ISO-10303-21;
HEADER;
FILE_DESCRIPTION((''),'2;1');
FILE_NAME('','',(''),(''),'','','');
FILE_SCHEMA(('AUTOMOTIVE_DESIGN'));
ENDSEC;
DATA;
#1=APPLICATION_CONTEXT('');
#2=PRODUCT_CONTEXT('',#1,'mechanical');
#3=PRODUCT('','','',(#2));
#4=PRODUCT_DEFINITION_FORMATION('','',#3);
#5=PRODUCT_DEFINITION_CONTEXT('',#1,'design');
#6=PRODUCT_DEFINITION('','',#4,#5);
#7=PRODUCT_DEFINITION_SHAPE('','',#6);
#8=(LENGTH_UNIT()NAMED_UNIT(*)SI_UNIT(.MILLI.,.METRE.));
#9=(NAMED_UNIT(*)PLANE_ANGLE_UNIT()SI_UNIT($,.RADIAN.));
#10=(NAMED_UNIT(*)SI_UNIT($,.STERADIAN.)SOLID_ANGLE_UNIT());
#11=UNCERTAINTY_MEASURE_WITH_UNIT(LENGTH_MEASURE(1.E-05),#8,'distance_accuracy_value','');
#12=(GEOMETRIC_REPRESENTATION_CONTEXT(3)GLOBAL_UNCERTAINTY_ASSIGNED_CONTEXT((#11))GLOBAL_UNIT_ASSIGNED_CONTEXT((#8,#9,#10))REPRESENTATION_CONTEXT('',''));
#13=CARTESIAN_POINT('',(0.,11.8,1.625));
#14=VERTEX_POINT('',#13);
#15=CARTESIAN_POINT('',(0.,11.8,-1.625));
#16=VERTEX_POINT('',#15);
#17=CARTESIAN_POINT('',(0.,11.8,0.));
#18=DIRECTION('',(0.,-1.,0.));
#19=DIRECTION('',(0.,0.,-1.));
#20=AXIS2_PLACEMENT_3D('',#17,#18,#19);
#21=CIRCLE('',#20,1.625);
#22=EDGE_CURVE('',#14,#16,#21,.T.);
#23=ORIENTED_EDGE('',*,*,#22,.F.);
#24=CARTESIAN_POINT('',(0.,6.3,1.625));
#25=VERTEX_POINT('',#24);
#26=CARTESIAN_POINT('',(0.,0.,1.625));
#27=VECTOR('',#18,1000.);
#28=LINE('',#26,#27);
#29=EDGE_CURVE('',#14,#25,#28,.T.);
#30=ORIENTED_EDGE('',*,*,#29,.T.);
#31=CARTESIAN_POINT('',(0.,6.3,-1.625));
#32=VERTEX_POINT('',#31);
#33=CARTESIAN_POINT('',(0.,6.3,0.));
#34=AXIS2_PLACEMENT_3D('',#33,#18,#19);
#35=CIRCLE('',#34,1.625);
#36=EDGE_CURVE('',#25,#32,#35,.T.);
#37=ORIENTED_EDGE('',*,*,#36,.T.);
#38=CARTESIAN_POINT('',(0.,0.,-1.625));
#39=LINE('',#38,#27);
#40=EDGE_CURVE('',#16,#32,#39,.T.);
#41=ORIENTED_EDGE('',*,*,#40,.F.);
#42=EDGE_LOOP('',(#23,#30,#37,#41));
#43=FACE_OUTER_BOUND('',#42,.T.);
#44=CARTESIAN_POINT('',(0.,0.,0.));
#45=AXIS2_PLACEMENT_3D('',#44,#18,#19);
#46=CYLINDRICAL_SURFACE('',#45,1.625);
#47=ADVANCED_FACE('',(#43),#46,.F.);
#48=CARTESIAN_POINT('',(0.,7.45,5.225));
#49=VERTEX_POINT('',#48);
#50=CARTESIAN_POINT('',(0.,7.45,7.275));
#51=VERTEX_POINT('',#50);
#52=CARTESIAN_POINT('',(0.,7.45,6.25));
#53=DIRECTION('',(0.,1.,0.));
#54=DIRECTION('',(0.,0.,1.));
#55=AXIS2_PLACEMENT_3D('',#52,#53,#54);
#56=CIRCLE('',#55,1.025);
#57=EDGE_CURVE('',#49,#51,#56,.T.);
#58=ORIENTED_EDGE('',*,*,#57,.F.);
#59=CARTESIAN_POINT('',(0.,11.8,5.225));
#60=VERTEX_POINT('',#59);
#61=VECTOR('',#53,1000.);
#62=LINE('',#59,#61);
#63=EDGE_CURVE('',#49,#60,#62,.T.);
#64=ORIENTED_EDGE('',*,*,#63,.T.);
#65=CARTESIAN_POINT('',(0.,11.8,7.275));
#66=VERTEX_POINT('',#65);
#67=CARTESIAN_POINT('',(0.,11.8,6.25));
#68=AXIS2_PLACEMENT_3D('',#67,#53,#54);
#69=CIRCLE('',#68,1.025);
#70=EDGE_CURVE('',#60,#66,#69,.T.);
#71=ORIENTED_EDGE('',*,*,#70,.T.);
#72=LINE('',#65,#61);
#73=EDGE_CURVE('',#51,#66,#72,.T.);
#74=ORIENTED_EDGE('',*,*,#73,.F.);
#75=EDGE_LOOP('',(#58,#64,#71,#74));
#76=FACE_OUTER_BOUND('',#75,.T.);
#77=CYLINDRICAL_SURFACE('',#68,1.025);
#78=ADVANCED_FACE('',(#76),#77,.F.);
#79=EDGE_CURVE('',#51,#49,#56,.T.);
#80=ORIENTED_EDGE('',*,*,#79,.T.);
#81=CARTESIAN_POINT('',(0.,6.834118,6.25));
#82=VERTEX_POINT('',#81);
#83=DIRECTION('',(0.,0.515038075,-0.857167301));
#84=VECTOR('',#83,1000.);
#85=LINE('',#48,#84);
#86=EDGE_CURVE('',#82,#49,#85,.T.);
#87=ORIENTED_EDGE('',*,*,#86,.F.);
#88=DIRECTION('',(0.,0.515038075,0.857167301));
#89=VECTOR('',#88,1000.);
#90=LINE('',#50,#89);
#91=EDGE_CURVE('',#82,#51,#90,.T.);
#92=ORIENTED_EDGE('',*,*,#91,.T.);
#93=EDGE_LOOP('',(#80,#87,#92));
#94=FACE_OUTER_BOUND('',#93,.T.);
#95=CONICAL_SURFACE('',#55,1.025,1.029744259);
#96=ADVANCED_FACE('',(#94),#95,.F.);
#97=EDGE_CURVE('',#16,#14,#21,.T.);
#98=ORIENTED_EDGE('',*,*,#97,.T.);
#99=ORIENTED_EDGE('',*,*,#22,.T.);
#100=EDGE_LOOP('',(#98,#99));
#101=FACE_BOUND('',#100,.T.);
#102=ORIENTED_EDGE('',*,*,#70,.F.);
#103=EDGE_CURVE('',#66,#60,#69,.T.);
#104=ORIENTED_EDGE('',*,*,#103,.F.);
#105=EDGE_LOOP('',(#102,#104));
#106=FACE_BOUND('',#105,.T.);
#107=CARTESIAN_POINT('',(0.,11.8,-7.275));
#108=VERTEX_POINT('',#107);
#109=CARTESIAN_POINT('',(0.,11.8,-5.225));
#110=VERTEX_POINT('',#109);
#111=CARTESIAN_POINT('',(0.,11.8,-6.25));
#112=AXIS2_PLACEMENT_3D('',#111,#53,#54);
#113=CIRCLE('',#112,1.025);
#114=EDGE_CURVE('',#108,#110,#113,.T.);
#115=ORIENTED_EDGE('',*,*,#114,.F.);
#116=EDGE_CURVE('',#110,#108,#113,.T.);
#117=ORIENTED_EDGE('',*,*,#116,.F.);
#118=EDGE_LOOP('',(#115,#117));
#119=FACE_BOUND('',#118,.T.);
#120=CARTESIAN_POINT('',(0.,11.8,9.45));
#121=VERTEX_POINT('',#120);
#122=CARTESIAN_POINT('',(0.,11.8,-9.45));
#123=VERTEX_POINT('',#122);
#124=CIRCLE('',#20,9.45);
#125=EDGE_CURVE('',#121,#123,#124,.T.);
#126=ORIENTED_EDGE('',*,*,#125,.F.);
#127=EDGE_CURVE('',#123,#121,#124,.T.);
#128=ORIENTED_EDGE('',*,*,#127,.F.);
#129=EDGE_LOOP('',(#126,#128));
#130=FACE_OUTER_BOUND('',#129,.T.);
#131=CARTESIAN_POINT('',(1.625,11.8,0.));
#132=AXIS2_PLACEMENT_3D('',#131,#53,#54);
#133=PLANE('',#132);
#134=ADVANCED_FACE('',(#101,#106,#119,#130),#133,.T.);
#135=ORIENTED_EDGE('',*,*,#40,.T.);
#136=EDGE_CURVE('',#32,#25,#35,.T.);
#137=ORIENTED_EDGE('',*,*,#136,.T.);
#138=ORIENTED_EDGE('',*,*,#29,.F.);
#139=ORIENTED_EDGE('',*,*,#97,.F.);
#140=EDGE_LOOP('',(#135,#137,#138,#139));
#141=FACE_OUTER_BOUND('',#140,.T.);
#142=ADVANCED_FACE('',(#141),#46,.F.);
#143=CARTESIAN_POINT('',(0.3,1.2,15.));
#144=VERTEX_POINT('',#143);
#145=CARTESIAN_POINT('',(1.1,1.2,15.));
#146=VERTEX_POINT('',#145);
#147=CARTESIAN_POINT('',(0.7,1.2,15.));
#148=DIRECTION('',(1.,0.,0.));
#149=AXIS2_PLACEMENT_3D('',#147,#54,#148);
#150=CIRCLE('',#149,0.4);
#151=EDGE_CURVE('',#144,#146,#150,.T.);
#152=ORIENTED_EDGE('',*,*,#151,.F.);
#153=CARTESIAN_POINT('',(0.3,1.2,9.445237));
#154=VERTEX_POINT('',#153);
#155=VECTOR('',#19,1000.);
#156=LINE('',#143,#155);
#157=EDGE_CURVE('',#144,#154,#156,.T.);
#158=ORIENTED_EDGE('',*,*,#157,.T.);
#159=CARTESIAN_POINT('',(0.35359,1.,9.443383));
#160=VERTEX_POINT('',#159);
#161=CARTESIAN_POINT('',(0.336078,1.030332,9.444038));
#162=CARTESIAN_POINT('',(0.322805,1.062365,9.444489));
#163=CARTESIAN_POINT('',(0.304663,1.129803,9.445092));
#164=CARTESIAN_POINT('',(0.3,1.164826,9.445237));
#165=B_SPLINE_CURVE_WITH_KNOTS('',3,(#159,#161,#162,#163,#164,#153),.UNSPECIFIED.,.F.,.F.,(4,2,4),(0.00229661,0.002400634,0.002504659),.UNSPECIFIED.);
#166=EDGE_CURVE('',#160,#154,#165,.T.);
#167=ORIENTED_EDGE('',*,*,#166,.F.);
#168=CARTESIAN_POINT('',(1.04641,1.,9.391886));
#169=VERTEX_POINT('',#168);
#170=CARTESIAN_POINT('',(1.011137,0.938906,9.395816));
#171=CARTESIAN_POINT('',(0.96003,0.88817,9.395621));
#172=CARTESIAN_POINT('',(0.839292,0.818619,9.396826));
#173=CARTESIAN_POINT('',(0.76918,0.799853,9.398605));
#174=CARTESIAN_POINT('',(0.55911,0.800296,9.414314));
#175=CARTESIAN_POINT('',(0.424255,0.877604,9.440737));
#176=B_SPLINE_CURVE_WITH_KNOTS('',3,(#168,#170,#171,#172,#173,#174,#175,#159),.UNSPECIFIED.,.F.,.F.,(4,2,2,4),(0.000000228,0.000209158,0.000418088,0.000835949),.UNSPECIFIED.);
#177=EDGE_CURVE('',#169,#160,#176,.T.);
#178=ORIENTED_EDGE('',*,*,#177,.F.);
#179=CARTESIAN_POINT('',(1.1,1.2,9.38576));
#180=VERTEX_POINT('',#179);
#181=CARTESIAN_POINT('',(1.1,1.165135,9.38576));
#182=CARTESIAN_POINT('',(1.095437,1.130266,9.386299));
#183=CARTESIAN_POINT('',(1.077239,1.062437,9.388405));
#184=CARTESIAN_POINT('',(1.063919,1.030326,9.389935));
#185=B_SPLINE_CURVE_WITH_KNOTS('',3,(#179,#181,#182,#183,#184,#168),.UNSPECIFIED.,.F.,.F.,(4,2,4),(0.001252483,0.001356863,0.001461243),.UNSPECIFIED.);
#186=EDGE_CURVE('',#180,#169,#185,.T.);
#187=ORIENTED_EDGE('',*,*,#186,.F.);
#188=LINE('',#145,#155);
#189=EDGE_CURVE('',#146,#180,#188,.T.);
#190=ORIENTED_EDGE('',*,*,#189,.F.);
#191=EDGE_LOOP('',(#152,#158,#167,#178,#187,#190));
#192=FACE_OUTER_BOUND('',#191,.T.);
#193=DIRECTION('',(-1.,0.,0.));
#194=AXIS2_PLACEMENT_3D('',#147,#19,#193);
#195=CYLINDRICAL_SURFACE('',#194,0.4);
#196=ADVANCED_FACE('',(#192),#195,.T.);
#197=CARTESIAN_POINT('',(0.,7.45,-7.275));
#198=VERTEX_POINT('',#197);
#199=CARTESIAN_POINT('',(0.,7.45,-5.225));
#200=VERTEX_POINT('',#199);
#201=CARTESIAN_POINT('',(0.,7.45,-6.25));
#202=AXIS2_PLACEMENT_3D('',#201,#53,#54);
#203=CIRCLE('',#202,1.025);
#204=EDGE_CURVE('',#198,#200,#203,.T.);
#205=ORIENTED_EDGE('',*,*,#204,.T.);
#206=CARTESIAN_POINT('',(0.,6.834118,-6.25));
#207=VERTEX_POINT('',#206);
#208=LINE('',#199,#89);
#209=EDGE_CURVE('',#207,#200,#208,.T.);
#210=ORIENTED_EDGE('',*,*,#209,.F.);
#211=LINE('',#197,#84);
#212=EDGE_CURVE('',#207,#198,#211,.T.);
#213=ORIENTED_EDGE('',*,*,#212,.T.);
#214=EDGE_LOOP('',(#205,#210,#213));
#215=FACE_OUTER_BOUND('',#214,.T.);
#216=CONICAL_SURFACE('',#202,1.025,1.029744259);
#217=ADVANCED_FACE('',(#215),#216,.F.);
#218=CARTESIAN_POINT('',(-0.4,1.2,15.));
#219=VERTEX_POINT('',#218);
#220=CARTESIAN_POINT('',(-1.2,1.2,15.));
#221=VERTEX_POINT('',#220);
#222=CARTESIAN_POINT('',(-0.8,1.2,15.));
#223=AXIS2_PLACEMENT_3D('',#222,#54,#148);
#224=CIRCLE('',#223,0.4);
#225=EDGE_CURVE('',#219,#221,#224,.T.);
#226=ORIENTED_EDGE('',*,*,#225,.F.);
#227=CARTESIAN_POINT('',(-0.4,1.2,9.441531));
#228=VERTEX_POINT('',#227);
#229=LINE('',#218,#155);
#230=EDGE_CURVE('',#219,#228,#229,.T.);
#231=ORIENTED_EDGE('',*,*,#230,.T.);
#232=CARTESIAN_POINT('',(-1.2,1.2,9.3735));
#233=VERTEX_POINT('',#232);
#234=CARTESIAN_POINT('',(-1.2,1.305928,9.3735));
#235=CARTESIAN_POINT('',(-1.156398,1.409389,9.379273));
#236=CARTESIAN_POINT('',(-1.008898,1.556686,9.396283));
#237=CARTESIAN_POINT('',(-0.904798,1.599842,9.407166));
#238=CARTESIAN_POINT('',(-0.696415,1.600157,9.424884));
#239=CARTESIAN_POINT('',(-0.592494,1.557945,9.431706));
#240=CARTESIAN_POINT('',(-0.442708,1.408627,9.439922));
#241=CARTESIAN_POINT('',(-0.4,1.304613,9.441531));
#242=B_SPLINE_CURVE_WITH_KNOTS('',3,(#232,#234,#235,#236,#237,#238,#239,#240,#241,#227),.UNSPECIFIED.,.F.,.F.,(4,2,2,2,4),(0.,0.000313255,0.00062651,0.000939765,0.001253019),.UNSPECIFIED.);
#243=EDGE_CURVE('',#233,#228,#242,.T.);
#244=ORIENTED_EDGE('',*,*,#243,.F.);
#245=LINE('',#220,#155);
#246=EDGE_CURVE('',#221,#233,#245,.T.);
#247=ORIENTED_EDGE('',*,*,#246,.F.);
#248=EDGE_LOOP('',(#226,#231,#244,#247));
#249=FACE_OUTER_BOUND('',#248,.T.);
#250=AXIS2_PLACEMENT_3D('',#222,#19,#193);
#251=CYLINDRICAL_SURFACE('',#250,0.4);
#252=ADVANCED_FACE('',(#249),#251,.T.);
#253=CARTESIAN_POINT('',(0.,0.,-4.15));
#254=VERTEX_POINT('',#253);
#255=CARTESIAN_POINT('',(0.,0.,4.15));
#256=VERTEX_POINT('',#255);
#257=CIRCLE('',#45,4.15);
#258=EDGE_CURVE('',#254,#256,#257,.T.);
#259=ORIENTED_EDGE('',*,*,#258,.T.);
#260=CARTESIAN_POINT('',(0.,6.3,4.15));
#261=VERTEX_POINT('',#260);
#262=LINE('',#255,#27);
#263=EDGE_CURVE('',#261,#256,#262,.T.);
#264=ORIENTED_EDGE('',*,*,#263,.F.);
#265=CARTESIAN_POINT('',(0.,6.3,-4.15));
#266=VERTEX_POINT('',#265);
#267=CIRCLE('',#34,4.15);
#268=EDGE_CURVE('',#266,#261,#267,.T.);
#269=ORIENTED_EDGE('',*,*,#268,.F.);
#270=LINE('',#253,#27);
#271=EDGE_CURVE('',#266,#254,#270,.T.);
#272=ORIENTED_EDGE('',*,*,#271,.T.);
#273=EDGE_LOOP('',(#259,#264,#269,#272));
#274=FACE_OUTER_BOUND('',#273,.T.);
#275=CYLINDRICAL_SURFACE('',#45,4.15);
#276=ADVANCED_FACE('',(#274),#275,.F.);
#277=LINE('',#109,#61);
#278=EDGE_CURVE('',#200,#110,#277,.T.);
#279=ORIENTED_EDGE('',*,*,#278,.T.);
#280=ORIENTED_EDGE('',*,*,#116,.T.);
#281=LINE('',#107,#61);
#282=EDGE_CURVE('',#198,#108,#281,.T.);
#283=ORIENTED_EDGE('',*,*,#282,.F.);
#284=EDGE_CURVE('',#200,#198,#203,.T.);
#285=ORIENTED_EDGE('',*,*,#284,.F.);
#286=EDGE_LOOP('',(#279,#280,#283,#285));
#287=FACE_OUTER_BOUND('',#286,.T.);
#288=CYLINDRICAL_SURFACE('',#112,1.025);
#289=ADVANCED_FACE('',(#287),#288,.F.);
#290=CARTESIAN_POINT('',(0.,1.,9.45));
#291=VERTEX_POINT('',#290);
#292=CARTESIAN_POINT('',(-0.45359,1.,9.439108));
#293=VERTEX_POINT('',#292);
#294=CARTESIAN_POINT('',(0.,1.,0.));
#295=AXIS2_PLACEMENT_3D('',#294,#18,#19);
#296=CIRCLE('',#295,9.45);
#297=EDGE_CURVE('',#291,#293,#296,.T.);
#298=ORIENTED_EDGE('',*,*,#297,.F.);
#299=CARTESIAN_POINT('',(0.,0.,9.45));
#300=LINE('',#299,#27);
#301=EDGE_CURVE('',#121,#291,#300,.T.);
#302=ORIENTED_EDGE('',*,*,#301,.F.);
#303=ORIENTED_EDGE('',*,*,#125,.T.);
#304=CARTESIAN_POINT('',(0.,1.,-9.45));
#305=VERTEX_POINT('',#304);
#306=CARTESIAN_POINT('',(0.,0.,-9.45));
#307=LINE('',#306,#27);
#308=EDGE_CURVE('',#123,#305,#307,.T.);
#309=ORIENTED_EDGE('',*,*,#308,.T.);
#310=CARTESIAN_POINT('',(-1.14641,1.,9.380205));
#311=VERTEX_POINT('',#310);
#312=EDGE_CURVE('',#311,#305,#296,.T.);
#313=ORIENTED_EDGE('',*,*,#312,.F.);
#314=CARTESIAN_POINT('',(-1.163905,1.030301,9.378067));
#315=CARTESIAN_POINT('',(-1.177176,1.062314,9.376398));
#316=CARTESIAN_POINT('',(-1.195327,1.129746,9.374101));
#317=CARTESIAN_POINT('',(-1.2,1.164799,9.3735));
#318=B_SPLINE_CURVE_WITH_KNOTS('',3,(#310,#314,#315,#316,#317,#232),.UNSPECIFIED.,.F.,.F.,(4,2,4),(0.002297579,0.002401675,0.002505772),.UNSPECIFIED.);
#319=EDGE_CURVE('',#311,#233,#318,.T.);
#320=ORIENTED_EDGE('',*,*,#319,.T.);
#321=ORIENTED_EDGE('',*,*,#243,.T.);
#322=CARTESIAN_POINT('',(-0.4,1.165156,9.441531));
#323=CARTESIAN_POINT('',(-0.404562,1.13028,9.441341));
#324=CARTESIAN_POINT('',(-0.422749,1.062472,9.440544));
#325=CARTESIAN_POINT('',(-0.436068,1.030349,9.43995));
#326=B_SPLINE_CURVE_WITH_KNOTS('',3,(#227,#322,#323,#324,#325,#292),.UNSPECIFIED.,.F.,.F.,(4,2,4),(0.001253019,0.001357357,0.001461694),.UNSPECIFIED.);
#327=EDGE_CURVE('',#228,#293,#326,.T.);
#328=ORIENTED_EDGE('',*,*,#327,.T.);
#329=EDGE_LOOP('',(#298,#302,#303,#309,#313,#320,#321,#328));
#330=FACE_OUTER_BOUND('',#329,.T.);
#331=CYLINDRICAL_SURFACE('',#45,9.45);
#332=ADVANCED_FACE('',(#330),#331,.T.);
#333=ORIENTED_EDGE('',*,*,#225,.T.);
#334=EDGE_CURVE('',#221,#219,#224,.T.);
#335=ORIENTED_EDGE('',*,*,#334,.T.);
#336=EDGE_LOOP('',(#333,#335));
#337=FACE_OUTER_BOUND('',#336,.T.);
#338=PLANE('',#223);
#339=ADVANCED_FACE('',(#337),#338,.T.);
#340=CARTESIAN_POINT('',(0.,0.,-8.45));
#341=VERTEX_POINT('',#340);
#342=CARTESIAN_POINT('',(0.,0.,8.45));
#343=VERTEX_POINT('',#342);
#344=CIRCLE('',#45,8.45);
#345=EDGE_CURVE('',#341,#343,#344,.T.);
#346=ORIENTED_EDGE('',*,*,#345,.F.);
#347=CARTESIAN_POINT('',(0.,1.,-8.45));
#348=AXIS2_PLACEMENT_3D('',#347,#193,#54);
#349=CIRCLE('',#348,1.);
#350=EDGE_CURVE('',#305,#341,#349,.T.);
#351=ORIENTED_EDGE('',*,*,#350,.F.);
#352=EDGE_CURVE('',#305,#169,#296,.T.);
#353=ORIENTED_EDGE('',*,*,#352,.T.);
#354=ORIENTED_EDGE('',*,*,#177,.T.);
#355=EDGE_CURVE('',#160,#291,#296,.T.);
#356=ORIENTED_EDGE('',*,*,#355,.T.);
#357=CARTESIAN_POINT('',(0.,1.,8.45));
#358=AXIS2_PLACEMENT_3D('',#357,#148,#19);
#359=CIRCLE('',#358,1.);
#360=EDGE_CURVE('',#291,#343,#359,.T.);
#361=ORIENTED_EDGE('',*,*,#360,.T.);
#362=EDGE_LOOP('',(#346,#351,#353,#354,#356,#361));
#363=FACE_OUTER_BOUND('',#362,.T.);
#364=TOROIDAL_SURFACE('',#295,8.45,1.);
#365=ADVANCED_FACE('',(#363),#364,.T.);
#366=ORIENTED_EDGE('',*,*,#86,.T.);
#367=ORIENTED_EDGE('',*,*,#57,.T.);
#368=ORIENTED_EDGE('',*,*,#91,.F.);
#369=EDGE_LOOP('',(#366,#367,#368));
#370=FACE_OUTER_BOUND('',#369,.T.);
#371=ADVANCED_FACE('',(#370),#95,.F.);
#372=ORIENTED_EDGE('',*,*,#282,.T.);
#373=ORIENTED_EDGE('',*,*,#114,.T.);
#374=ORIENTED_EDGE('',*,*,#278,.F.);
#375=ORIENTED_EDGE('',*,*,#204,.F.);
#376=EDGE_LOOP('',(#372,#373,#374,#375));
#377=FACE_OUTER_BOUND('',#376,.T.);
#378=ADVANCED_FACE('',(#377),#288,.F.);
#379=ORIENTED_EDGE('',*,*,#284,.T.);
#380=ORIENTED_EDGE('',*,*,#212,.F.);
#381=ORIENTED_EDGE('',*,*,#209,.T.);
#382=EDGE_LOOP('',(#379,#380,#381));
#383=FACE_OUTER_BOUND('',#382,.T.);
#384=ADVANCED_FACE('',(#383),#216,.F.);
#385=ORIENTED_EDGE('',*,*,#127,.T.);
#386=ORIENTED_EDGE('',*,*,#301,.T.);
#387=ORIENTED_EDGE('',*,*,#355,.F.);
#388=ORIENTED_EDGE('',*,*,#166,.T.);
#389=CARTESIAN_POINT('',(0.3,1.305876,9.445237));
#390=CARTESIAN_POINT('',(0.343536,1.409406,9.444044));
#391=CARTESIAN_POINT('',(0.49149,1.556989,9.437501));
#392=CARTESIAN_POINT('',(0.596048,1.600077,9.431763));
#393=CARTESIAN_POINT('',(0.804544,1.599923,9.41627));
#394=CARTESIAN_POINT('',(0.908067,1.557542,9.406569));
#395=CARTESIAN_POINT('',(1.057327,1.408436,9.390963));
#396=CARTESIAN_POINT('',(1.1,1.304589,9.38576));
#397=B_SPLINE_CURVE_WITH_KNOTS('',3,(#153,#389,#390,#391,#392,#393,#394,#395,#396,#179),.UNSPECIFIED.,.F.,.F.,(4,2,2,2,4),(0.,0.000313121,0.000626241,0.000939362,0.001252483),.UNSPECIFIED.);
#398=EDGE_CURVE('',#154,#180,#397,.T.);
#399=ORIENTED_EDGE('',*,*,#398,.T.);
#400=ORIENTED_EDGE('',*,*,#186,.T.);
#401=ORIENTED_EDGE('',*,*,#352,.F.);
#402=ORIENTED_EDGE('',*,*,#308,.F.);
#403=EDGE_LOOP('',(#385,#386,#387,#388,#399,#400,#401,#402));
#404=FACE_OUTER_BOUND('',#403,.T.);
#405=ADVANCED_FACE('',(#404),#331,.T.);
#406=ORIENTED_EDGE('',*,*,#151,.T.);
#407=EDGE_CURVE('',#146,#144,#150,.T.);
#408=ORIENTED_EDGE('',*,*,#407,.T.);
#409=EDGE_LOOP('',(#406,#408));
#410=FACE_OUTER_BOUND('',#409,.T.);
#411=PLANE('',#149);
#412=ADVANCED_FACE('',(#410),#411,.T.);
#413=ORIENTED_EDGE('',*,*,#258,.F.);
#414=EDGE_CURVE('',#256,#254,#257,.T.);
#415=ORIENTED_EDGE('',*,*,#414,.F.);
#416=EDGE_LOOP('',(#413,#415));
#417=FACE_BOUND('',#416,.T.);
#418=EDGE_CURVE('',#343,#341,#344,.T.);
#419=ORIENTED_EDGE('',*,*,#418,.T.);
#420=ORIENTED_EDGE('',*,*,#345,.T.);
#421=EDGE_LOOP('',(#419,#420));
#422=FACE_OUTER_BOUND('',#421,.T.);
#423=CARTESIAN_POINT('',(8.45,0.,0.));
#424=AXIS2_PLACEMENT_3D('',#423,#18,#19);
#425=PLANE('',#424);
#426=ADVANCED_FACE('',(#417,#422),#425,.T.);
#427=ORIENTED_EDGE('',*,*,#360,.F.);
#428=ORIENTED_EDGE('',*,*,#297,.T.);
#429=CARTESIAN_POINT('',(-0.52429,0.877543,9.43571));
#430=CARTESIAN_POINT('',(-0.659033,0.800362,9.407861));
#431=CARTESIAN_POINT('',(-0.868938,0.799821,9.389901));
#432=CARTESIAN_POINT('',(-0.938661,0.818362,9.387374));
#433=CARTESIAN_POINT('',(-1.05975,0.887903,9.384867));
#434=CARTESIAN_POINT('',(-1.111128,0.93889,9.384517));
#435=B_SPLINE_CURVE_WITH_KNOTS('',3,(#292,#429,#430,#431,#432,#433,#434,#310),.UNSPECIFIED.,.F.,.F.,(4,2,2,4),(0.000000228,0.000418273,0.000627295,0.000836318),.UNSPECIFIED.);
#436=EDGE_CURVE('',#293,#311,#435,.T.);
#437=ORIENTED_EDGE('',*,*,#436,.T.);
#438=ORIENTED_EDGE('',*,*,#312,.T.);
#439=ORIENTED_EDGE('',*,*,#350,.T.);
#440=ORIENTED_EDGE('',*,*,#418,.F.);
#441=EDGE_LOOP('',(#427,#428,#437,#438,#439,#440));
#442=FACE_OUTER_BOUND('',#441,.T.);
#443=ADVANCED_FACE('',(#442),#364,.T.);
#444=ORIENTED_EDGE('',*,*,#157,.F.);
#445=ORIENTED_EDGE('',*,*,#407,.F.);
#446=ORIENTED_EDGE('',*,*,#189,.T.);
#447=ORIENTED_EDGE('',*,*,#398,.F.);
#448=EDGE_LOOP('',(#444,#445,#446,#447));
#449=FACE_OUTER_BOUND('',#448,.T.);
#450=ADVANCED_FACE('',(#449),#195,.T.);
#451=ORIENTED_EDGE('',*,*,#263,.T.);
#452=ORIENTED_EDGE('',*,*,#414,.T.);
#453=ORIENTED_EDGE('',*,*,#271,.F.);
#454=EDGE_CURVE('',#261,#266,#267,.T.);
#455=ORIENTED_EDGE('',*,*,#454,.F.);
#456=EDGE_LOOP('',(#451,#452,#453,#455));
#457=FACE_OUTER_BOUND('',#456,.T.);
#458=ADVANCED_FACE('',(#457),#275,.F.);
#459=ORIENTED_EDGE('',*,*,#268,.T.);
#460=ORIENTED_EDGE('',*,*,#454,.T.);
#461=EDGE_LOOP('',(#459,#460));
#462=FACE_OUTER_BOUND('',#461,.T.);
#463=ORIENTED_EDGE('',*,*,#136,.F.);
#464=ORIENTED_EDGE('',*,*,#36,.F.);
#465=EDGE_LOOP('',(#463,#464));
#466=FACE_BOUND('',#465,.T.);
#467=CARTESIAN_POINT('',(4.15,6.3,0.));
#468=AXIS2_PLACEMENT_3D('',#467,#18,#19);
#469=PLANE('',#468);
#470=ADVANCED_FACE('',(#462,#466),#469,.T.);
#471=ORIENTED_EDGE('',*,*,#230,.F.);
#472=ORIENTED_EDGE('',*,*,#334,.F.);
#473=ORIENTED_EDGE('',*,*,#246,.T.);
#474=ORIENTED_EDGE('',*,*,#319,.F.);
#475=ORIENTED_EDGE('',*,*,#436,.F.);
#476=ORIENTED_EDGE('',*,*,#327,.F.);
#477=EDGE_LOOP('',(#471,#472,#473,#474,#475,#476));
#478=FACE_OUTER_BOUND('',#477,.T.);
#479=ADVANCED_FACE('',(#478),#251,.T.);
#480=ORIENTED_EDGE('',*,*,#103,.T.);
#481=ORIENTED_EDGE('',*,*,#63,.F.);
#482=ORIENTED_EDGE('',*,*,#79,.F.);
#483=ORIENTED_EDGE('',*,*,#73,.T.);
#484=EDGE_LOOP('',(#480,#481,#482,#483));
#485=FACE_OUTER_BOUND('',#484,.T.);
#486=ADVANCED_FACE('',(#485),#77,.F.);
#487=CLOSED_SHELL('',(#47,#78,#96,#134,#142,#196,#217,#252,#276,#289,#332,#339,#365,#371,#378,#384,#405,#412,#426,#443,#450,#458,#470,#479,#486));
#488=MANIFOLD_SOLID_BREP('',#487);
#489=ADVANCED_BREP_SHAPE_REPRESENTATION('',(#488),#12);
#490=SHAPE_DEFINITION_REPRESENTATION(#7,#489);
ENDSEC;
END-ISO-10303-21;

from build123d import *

# Parameters (mm, degrees)
M2_5_TAPPED_HOLE1_D     = 2.05
M2_5_TAPPED_HOLE1_DEPTH = 4.35
M2_5_TAPPED_HOLE1_TIP   = 0.615882135
SKETCH5_R               = 0.4
BOSS_EXTRUDE1_DEPTH     = 15
SKETCH6_R               = 4.15
CUT_EXTRUDE2_DEPTH      = 15


with BuildPart() as part:
    # Sketch1 → Revolve1 (revolve)
    with BuildSketch(Plane.XY, mode=Mode.PRIVATE) as revolve1_sk:
        with BuildLine():
            Line((1.625, 11.8), (9.45, 11.8))
            Line((9.45, 11.8), (9.45, 1))
            ThreePointArc((9.45, 1), (9.157106781, 0.292893219), (8.45, 0))
            Line((8.45, 0), (4.15, 0))
            Line((4.15, 0), (4.15, 6.3))
            Line((4.15, 6.3), (1.625, 6.3))
            Line((1.625, 6.3), (1.625, 11.8))
        make_face()
    revolve(revolve1_sk.sketch.rotate(Axis((0, 0, 0), (0, 1, 0)), 90), axis=Axis((0, 0, 0), (0, 1, 0)))

    # M2.5 Tapped Hole1
    with Locations(Plane(origin=(0, 11.8, 0), x_dir=(-1, 0, 0), z_dir=(0, 1, 0))):
        with Locations((0, -6.25), (0, 6.25)):
            Hole(M2_5_TAPPED_HOLE1_D / 2, depth=M2_5_TAPPED_HOLE1_DEPTH)
            with Locations((0, 0, -(M2_5_TAPPED_HOLE1_DEPTH + M2_5_TAPPED_HOLE1_TIP / 2))):  # 118° drill point
                Cone(0, M2_5_TAPPED_HOLE1_D / 2, M2_5_TAPPED_HOLE1_TIP, mode=Mode.SUBTRACT)

    # Sketch5 → Boss-Extrude1 (add)
    with BuildSketch(Plane.XY):
        with Locations(Location((-0.8, 1.2, 0), (0, 0, 180))):
            Circle(SKETCH5_R)
        with Locations(Location((0.7, 1.2, 0), (0, 0, 180))):
            Circle(SKETCH5_R)
    extrude(amount=BOSS_EXTRUDE1_DEPTH)

    # Sketch6 → Cut-Extrude2 (cut)
    with BuildSketch(Plane.XZ.offset(-6.3)):
        with Locations(Location((0, 0, 0), (0, 0, 270))):
            Circle(SKETCH6_R)
    extrude(amount=CUT_EXTRUDE2_DEPTH, mode=Mode.SUBTRACT)


solid = part.part
